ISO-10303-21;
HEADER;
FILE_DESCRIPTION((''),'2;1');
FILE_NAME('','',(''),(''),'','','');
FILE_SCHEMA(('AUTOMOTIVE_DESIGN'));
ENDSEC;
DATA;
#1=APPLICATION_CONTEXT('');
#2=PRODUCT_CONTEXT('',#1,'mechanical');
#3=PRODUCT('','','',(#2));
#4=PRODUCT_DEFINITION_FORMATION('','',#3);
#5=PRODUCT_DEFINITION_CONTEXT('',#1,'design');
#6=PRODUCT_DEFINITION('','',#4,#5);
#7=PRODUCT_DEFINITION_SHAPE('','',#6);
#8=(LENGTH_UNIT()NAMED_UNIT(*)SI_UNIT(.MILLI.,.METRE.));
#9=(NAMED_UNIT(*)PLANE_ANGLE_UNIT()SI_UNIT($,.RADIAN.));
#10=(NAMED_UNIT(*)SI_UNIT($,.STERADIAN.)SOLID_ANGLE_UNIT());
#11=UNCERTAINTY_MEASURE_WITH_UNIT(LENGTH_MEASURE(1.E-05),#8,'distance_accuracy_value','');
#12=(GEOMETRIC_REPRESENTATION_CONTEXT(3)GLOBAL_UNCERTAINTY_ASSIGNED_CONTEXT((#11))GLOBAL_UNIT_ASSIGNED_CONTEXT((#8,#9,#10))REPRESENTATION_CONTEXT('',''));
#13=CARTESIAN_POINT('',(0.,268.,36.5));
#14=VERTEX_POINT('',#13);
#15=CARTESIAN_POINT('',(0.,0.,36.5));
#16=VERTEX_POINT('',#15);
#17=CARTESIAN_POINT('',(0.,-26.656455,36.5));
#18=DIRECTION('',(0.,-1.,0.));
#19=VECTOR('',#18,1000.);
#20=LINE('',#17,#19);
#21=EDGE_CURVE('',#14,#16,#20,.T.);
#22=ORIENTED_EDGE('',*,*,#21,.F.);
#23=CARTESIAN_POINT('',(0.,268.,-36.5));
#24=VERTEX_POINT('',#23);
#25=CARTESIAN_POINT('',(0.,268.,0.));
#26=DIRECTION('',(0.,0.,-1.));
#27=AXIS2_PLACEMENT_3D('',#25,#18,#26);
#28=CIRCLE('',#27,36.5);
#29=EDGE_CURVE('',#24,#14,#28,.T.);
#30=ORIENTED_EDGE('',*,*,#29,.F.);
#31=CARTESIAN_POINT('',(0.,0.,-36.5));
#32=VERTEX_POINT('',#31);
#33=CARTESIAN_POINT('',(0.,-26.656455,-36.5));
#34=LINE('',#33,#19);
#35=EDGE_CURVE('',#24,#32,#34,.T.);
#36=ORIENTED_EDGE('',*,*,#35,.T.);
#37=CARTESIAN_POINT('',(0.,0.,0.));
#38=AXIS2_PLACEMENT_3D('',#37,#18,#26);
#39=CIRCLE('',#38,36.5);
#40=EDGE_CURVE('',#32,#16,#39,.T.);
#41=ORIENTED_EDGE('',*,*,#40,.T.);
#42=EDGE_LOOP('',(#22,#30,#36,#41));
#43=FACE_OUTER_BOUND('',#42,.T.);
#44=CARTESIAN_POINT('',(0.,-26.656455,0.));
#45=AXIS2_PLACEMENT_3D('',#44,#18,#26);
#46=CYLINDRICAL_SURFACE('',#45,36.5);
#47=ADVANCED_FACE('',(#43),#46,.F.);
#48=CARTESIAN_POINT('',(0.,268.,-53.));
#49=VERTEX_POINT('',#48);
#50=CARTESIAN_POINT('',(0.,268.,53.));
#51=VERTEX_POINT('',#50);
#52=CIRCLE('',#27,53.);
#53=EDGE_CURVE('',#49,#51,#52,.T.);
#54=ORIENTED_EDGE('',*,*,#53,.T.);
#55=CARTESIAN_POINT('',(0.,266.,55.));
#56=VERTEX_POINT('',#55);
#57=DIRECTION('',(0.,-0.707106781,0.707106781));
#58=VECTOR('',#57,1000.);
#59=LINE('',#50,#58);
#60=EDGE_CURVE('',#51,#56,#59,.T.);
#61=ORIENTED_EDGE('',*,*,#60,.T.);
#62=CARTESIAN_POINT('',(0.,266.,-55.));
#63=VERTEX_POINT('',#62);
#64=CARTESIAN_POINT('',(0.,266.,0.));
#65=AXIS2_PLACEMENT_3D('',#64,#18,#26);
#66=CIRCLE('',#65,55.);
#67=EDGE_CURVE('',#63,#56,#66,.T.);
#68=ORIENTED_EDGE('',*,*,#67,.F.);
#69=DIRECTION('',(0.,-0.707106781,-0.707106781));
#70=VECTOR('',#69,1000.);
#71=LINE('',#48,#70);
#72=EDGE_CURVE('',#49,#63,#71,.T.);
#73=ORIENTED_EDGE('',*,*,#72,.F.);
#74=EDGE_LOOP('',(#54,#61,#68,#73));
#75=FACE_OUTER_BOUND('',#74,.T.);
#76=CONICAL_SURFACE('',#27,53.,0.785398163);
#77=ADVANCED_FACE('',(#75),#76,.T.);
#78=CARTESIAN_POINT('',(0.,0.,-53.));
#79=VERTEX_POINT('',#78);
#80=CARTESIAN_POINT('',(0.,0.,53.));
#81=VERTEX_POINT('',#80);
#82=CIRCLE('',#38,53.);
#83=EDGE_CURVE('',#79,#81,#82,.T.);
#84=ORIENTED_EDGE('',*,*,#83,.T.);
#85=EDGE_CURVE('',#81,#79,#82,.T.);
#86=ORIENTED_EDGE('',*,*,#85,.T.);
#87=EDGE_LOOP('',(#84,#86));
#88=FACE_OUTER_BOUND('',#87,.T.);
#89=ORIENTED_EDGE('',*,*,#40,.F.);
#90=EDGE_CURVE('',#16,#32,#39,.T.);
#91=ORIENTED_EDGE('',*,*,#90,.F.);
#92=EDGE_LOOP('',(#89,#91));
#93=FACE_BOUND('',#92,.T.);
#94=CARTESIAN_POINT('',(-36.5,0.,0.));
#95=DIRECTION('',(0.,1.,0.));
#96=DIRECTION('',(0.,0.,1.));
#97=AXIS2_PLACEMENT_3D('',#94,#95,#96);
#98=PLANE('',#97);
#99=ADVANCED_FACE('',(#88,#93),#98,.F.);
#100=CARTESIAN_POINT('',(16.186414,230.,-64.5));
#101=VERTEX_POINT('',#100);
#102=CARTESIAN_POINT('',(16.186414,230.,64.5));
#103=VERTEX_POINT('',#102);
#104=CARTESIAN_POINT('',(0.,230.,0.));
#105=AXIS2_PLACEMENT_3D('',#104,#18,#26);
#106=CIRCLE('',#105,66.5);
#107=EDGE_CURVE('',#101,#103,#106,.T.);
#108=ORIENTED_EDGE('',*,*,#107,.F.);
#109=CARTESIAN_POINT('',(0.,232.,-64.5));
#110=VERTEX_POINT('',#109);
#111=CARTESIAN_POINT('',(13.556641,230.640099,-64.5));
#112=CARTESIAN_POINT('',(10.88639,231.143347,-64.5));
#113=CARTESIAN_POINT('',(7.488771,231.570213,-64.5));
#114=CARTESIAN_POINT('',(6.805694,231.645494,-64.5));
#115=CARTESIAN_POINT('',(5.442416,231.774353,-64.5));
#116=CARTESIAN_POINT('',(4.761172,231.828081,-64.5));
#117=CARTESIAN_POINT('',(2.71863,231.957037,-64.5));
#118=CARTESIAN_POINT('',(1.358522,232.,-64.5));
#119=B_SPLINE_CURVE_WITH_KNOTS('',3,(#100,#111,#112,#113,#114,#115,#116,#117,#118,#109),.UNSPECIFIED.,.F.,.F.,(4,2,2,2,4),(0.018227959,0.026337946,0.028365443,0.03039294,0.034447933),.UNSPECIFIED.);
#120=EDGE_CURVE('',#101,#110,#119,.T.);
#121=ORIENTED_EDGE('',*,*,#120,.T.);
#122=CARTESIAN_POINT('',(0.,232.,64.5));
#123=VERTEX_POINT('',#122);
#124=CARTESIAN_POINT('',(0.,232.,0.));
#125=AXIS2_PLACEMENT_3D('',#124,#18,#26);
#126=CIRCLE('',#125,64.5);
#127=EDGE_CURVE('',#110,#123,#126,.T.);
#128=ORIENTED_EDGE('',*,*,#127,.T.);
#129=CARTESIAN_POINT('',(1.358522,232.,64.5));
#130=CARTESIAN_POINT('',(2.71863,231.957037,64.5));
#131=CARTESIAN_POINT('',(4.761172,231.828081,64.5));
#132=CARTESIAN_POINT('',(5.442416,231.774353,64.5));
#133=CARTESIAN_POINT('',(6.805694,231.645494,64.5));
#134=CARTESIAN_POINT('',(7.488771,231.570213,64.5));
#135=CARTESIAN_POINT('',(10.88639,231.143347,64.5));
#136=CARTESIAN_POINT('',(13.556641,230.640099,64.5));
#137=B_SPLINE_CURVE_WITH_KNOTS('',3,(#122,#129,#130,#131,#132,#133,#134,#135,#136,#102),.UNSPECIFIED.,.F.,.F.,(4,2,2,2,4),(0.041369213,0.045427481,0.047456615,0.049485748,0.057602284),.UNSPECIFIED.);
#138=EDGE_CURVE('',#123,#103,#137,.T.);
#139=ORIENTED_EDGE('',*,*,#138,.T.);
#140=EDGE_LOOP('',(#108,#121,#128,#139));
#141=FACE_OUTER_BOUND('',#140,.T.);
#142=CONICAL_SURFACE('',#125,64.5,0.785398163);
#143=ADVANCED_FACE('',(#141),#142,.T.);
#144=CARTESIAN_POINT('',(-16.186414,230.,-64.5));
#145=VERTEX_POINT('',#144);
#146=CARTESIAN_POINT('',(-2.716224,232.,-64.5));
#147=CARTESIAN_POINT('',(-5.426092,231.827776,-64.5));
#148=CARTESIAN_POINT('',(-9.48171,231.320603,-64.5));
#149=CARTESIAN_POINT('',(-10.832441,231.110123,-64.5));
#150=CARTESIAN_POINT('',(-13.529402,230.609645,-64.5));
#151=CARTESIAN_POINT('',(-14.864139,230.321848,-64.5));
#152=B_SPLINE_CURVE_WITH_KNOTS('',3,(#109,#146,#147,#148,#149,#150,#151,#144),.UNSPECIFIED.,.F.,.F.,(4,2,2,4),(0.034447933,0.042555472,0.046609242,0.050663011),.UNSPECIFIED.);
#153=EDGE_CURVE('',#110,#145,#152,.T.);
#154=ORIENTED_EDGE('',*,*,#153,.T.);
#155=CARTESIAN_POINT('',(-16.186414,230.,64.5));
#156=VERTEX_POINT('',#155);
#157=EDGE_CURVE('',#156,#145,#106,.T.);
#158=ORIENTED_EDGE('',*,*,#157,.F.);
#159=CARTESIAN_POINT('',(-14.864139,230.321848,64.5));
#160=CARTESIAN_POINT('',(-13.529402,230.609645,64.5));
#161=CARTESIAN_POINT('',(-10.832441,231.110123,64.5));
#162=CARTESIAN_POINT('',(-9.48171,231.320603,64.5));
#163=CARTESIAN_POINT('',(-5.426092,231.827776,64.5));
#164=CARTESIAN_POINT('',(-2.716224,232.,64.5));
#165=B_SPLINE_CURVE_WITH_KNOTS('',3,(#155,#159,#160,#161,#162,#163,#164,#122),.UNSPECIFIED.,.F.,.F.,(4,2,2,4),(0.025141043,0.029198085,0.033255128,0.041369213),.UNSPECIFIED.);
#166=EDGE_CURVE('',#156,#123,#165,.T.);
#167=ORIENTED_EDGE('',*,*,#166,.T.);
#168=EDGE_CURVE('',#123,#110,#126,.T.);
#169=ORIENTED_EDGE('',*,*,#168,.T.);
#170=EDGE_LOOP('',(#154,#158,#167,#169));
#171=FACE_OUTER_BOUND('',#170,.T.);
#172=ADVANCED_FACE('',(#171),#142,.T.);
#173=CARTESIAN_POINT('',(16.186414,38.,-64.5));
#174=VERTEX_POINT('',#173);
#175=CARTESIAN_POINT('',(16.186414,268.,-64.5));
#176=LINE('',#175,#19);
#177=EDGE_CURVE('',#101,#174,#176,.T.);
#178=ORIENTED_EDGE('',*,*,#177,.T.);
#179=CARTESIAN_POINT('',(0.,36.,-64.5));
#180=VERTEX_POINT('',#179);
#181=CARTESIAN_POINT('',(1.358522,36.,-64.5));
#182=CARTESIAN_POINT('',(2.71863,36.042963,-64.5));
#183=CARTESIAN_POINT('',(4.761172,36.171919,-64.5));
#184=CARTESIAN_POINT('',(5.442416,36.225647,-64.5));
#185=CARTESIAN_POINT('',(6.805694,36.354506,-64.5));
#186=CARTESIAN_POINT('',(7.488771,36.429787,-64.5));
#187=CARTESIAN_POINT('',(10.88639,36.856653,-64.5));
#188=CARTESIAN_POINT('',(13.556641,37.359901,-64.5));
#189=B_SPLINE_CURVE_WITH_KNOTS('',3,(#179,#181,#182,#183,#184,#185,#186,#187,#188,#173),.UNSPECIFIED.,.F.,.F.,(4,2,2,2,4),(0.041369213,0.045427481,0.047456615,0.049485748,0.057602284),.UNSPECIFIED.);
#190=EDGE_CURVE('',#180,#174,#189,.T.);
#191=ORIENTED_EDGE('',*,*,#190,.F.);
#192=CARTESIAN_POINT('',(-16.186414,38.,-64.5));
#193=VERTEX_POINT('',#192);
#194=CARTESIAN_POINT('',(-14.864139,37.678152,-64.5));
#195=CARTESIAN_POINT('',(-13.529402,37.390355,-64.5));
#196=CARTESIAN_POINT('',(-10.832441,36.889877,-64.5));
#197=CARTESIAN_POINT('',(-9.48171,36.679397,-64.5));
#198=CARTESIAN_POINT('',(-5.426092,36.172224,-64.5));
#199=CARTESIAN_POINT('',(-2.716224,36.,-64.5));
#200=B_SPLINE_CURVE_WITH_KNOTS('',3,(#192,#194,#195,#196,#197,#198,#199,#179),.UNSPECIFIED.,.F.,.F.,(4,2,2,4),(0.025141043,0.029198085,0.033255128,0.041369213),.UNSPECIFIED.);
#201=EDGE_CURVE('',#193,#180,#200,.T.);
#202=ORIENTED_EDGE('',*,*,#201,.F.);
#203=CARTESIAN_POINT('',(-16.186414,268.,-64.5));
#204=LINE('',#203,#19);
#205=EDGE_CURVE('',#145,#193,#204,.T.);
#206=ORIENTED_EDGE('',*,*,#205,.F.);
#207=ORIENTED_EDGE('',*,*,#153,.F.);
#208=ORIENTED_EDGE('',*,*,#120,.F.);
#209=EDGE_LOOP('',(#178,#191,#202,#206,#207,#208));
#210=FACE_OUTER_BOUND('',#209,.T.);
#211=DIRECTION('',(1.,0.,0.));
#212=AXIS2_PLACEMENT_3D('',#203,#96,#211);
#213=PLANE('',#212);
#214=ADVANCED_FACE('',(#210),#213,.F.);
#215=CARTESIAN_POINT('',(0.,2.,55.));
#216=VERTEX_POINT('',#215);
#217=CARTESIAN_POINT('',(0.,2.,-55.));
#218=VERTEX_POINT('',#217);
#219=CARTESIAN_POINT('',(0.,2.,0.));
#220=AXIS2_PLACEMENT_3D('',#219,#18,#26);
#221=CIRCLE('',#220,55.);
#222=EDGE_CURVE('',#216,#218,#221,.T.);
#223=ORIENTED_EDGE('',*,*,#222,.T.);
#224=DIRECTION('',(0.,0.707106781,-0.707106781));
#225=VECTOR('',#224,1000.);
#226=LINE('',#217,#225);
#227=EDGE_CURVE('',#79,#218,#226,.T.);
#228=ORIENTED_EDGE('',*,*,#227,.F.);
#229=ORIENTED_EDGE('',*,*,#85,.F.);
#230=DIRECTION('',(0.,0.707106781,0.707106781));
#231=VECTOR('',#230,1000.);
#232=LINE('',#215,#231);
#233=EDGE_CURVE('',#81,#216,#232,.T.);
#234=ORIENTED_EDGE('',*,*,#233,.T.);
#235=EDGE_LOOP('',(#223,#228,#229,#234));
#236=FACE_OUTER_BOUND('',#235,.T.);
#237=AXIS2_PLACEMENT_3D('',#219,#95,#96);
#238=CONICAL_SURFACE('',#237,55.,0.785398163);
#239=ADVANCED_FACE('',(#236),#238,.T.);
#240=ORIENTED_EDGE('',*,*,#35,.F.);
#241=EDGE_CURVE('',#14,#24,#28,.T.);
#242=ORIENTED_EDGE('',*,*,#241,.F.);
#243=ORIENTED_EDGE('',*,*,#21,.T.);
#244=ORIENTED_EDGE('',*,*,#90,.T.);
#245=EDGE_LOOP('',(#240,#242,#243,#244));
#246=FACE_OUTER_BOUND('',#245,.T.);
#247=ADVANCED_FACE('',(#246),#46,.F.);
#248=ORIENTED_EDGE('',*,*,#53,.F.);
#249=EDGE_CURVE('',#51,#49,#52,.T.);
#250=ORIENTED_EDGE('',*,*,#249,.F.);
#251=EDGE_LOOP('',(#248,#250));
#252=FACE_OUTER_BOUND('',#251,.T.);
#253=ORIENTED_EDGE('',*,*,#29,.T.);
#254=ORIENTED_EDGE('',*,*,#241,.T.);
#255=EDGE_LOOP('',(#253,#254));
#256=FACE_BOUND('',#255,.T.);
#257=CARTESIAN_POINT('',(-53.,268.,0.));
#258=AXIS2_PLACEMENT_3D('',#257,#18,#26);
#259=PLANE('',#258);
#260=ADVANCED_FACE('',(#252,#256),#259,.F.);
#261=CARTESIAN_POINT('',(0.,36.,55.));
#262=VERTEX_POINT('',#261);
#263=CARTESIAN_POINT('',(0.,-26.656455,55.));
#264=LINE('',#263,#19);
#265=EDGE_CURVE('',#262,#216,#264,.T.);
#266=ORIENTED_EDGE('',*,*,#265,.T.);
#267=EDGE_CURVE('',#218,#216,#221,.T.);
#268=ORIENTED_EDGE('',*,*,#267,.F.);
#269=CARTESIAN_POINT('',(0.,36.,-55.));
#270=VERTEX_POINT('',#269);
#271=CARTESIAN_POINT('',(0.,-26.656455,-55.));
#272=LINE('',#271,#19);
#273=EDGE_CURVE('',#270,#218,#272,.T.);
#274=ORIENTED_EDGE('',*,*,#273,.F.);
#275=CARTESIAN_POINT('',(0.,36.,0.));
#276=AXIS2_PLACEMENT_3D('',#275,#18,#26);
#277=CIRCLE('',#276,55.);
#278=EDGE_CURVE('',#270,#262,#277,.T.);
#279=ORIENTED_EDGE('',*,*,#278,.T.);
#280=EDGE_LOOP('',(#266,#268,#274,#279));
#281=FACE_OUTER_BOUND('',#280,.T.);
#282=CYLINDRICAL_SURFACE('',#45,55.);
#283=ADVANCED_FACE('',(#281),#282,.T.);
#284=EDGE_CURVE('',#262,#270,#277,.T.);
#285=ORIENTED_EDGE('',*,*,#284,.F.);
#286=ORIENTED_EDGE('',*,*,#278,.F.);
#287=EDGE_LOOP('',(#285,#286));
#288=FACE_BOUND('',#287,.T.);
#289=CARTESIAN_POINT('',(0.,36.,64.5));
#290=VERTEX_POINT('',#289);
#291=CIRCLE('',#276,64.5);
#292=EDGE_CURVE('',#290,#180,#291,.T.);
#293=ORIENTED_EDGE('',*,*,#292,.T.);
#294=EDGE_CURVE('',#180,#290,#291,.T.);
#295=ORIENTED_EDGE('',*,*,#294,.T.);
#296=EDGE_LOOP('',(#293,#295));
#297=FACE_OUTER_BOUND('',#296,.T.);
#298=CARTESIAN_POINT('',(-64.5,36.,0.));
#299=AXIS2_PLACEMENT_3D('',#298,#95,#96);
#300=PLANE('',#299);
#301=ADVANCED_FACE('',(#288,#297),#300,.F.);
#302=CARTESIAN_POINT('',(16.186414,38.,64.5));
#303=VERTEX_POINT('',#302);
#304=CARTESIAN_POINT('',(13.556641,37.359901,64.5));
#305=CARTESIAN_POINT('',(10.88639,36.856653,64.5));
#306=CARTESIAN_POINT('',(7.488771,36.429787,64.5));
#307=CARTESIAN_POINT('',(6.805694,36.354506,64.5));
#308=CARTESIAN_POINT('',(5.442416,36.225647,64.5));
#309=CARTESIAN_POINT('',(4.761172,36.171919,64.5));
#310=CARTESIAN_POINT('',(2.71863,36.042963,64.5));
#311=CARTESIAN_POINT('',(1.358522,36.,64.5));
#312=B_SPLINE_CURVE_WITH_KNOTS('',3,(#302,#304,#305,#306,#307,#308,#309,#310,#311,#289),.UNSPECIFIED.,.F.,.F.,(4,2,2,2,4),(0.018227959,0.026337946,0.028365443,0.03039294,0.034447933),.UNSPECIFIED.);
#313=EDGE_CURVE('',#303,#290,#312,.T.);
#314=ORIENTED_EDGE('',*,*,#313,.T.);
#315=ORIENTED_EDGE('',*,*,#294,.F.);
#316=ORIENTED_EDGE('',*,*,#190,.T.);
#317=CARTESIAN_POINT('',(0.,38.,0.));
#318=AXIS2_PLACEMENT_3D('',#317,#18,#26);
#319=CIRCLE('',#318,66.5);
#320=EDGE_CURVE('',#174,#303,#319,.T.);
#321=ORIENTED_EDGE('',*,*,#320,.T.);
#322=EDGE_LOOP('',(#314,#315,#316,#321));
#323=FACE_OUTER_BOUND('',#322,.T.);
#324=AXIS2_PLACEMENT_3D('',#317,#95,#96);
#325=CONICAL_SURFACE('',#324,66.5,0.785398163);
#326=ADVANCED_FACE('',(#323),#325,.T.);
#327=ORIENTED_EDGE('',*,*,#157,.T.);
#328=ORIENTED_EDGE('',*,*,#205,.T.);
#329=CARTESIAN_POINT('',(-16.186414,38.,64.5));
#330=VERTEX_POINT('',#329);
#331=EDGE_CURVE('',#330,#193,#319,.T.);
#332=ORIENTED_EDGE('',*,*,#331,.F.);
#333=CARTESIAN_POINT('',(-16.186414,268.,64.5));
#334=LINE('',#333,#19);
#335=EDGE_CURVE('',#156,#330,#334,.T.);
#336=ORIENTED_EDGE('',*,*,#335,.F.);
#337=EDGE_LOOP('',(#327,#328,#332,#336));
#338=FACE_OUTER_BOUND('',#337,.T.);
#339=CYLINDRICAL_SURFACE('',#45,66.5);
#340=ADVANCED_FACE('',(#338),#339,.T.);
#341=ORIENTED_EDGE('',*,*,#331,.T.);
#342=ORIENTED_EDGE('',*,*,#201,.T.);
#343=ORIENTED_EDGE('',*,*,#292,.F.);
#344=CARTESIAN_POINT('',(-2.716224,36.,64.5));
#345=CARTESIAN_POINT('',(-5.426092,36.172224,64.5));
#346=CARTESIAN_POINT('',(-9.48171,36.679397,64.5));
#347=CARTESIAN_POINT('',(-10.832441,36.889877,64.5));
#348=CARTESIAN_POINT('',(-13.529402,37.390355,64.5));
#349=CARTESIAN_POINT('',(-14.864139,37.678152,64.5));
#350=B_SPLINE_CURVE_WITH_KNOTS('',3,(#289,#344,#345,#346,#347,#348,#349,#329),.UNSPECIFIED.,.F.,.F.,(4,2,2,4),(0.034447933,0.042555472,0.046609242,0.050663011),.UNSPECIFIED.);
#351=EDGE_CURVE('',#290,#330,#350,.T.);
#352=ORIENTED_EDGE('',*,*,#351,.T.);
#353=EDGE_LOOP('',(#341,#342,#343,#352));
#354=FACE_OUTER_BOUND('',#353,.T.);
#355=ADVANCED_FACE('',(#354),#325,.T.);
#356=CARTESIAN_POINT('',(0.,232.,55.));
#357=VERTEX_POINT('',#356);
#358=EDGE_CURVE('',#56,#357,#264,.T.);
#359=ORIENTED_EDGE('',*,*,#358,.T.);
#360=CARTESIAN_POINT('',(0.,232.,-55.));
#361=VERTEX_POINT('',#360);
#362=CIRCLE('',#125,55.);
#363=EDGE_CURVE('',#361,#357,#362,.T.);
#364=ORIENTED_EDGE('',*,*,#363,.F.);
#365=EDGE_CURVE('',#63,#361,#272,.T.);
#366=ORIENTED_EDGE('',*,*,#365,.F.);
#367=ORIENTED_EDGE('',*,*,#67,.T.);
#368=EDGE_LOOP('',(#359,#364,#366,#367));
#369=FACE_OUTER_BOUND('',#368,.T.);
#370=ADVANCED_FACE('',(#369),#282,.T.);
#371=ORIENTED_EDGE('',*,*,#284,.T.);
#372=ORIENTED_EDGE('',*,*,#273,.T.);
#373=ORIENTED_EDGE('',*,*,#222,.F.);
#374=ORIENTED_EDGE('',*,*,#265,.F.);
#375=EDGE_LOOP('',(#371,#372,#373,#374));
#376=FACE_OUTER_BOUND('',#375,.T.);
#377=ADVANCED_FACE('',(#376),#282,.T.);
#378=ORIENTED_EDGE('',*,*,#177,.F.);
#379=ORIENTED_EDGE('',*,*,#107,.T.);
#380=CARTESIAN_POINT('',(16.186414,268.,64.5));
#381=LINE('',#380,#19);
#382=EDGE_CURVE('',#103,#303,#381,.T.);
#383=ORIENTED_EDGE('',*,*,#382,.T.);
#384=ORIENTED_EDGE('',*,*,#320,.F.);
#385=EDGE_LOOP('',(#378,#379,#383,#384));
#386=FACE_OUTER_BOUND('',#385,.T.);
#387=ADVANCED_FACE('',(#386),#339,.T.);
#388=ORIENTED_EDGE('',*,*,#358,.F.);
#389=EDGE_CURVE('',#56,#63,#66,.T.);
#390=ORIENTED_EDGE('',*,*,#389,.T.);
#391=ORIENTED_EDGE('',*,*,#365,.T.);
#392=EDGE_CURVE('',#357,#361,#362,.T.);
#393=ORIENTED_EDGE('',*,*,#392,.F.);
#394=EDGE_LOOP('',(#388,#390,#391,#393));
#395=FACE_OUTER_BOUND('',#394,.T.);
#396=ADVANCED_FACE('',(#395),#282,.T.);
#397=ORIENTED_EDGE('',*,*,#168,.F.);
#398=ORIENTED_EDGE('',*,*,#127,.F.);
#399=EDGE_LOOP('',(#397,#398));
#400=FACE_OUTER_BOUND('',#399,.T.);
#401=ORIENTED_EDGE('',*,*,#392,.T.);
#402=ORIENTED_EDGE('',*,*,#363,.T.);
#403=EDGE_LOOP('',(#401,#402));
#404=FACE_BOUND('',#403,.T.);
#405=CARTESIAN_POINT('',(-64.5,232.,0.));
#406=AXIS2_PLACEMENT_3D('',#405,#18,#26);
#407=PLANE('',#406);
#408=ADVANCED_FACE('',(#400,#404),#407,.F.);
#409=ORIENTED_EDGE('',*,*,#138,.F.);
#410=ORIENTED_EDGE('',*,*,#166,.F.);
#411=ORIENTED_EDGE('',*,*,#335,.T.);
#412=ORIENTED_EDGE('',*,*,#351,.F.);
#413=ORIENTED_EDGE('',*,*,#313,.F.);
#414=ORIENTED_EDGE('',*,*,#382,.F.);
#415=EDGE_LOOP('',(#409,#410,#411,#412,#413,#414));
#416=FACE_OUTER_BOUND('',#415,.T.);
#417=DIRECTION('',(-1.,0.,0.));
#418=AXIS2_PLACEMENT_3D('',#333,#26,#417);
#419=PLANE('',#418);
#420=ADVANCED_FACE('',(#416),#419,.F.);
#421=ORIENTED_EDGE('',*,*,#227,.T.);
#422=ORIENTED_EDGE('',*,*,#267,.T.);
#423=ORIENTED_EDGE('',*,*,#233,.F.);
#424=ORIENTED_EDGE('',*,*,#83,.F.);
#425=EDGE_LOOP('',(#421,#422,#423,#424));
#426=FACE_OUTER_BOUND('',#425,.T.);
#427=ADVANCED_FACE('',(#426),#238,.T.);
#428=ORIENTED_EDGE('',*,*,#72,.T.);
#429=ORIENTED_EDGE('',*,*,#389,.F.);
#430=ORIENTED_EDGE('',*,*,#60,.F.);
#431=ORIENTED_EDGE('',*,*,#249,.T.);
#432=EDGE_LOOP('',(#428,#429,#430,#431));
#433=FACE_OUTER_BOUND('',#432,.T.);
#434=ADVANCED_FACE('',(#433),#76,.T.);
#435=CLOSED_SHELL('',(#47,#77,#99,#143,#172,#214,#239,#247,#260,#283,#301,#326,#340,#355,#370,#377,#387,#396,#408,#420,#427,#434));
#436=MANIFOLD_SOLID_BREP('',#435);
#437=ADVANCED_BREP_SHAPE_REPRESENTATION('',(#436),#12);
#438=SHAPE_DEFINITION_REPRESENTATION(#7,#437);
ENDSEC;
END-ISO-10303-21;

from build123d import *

# Parameters (mm, degrees)
CUT_EXTRUDE1_DEPTH = 251.336773168


with BuildPart() as part:
    # Sketch1 → Revolve1 (revolve)
    with BuildSketch(Plane.XY, mode=Mode.PRIVATE) as revolve1_sk:
        Polygon((-66.5, 230), (-66.5, 38), (-64.5, 36), (-55, 36), (-55, 2), (-53, 0), (-36.5, 0), (-36.5, 268), (-53, 268), (-55, 266), (-55, 232), (-64.5, 232), align=None)
    revolve(revolve1_sk.sketch.rotate(Axis((0, -26.656454657, 0), (0, 1, 0)), 270), axis=Axis((0, -26.656454657, 0), (0, 1, 0)))

    # Sketch2 → Cut-Extrude1 (cut, through all)
    with BuildSketch(Plane.XZ.offset(-36)):
        with BuildLine():
            Line((-16.186414056, 64.5), (16.186414056, 64.5))
            ThreePointArc((16.186414056, 64.5), (0, 66.5), (-16.186414056, 64.5))
        make_face()
        with BuildLine():
            Line((-16.186414056, -64.5), (16.186414056, -64.5))
            ThreePointArc((16.186414056, -64.5), (0, -66.5), (-16.186414056, -64.5))
        make_face()
    extrude(amount=-CUT_EXTRUDE1_DEPTH, mode=Mode.SUBTRACT)


solid = part.part
